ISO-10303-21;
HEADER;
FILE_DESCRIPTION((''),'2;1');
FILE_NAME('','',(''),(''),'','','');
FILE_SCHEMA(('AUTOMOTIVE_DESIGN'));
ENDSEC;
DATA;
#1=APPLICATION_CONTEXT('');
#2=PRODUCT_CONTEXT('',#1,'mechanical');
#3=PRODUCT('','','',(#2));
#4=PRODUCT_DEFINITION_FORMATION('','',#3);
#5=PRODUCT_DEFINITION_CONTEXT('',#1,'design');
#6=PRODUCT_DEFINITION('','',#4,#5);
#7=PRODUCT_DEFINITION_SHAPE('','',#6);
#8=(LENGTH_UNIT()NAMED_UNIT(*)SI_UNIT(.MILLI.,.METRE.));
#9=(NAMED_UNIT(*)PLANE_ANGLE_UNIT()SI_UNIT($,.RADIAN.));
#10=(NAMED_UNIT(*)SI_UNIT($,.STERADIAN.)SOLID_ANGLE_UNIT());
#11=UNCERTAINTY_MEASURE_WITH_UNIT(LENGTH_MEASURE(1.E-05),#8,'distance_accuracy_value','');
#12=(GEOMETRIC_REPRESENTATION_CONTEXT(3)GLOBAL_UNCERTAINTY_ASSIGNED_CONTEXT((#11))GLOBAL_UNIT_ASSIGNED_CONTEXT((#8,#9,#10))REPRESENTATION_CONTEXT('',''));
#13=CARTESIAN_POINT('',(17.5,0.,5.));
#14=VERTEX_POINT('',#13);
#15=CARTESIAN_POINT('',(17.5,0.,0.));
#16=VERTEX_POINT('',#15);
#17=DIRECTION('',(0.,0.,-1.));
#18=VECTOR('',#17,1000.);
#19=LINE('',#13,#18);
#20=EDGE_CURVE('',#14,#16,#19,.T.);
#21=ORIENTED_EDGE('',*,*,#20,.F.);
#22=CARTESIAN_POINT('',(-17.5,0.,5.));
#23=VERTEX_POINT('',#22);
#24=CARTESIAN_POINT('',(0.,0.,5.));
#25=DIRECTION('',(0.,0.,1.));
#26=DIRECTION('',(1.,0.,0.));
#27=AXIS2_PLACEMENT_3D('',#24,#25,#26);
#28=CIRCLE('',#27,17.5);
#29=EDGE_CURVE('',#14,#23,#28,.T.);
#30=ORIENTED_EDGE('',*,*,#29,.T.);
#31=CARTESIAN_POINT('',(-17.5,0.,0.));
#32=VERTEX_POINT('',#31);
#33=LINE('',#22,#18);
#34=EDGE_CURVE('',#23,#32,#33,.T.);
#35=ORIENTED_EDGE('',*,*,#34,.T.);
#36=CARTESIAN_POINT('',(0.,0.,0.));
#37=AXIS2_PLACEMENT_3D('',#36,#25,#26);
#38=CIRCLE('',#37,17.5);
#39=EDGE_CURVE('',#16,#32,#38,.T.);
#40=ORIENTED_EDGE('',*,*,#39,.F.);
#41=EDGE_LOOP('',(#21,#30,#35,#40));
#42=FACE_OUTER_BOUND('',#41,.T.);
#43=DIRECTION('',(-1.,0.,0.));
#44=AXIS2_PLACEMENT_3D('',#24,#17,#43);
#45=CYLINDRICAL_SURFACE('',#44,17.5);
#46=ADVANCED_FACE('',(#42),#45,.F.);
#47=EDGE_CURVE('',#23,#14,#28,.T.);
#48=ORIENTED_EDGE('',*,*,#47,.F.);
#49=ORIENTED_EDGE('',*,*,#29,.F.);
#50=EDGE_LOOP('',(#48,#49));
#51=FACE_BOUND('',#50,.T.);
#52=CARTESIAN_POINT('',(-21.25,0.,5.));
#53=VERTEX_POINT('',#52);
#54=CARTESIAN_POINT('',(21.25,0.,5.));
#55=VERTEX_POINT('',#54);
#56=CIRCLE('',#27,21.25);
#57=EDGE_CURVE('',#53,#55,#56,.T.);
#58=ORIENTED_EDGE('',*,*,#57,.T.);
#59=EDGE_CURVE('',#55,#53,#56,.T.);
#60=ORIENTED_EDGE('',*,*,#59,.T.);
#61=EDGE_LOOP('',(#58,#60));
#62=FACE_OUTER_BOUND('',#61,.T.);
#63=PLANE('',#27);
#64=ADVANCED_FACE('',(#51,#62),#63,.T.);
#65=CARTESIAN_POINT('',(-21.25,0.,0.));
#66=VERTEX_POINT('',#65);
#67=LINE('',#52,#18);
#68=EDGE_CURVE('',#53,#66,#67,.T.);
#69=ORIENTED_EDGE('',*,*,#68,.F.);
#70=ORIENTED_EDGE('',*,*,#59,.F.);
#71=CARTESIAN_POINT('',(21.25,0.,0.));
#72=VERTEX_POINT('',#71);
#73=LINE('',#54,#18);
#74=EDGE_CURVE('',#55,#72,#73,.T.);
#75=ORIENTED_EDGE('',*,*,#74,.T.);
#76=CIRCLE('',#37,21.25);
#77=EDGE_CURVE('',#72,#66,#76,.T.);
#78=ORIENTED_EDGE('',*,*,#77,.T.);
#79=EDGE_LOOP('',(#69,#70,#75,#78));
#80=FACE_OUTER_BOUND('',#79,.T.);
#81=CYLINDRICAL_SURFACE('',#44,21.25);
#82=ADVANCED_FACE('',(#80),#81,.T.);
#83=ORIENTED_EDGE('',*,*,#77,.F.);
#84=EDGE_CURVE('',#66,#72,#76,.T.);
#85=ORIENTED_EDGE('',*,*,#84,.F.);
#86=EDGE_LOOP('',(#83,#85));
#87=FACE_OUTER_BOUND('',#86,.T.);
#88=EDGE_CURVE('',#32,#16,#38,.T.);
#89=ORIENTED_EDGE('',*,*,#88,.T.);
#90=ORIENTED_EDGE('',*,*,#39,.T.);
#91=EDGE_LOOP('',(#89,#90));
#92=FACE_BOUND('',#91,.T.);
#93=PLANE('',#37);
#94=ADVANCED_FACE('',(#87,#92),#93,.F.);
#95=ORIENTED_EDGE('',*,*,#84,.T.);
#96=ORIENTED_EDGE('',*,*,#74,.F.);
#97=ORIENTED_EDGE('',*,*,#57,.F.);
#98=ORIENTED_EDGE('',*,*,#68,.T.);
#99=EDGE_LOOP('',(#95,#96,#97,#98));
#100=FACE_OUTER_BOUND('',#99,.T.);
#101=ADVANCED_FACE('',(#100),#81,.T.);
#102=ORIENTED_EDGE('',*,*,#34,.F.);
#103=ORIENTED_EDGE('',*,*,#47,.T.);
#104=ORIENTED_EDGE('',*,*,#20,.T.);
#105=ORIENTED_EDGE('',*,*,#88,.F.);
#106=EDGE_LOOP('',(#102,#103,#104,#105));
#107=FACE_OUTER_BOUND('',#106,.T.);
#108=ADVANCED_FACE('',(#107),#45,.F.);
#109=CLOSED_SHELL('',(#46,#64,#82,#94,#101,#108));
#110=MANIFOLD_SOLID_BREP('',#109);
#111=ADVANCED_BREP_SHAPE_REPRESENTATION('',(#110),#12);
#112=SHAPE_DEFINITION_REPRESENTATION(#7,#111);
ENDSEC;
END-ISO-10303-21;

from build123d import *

# Parameters (mm, degrees)
SKETCH_1_R      = 21.25
SKETCH_1_R_2    = 17.5
EXTRUDE_1_DEPTH = 5


with BuildPart() as part:
    # 草图1 → 凸台-拉伸1 (new body)
    with BuildSketch(Plane.XY):
        Circle(SKETCH_1_R)
        Circle(SKETCH_1_R_2, mode=Mode.SUBTRACT)
    extrude(amount=EXTRUDE_1_DEPTH)


solid = part.part
